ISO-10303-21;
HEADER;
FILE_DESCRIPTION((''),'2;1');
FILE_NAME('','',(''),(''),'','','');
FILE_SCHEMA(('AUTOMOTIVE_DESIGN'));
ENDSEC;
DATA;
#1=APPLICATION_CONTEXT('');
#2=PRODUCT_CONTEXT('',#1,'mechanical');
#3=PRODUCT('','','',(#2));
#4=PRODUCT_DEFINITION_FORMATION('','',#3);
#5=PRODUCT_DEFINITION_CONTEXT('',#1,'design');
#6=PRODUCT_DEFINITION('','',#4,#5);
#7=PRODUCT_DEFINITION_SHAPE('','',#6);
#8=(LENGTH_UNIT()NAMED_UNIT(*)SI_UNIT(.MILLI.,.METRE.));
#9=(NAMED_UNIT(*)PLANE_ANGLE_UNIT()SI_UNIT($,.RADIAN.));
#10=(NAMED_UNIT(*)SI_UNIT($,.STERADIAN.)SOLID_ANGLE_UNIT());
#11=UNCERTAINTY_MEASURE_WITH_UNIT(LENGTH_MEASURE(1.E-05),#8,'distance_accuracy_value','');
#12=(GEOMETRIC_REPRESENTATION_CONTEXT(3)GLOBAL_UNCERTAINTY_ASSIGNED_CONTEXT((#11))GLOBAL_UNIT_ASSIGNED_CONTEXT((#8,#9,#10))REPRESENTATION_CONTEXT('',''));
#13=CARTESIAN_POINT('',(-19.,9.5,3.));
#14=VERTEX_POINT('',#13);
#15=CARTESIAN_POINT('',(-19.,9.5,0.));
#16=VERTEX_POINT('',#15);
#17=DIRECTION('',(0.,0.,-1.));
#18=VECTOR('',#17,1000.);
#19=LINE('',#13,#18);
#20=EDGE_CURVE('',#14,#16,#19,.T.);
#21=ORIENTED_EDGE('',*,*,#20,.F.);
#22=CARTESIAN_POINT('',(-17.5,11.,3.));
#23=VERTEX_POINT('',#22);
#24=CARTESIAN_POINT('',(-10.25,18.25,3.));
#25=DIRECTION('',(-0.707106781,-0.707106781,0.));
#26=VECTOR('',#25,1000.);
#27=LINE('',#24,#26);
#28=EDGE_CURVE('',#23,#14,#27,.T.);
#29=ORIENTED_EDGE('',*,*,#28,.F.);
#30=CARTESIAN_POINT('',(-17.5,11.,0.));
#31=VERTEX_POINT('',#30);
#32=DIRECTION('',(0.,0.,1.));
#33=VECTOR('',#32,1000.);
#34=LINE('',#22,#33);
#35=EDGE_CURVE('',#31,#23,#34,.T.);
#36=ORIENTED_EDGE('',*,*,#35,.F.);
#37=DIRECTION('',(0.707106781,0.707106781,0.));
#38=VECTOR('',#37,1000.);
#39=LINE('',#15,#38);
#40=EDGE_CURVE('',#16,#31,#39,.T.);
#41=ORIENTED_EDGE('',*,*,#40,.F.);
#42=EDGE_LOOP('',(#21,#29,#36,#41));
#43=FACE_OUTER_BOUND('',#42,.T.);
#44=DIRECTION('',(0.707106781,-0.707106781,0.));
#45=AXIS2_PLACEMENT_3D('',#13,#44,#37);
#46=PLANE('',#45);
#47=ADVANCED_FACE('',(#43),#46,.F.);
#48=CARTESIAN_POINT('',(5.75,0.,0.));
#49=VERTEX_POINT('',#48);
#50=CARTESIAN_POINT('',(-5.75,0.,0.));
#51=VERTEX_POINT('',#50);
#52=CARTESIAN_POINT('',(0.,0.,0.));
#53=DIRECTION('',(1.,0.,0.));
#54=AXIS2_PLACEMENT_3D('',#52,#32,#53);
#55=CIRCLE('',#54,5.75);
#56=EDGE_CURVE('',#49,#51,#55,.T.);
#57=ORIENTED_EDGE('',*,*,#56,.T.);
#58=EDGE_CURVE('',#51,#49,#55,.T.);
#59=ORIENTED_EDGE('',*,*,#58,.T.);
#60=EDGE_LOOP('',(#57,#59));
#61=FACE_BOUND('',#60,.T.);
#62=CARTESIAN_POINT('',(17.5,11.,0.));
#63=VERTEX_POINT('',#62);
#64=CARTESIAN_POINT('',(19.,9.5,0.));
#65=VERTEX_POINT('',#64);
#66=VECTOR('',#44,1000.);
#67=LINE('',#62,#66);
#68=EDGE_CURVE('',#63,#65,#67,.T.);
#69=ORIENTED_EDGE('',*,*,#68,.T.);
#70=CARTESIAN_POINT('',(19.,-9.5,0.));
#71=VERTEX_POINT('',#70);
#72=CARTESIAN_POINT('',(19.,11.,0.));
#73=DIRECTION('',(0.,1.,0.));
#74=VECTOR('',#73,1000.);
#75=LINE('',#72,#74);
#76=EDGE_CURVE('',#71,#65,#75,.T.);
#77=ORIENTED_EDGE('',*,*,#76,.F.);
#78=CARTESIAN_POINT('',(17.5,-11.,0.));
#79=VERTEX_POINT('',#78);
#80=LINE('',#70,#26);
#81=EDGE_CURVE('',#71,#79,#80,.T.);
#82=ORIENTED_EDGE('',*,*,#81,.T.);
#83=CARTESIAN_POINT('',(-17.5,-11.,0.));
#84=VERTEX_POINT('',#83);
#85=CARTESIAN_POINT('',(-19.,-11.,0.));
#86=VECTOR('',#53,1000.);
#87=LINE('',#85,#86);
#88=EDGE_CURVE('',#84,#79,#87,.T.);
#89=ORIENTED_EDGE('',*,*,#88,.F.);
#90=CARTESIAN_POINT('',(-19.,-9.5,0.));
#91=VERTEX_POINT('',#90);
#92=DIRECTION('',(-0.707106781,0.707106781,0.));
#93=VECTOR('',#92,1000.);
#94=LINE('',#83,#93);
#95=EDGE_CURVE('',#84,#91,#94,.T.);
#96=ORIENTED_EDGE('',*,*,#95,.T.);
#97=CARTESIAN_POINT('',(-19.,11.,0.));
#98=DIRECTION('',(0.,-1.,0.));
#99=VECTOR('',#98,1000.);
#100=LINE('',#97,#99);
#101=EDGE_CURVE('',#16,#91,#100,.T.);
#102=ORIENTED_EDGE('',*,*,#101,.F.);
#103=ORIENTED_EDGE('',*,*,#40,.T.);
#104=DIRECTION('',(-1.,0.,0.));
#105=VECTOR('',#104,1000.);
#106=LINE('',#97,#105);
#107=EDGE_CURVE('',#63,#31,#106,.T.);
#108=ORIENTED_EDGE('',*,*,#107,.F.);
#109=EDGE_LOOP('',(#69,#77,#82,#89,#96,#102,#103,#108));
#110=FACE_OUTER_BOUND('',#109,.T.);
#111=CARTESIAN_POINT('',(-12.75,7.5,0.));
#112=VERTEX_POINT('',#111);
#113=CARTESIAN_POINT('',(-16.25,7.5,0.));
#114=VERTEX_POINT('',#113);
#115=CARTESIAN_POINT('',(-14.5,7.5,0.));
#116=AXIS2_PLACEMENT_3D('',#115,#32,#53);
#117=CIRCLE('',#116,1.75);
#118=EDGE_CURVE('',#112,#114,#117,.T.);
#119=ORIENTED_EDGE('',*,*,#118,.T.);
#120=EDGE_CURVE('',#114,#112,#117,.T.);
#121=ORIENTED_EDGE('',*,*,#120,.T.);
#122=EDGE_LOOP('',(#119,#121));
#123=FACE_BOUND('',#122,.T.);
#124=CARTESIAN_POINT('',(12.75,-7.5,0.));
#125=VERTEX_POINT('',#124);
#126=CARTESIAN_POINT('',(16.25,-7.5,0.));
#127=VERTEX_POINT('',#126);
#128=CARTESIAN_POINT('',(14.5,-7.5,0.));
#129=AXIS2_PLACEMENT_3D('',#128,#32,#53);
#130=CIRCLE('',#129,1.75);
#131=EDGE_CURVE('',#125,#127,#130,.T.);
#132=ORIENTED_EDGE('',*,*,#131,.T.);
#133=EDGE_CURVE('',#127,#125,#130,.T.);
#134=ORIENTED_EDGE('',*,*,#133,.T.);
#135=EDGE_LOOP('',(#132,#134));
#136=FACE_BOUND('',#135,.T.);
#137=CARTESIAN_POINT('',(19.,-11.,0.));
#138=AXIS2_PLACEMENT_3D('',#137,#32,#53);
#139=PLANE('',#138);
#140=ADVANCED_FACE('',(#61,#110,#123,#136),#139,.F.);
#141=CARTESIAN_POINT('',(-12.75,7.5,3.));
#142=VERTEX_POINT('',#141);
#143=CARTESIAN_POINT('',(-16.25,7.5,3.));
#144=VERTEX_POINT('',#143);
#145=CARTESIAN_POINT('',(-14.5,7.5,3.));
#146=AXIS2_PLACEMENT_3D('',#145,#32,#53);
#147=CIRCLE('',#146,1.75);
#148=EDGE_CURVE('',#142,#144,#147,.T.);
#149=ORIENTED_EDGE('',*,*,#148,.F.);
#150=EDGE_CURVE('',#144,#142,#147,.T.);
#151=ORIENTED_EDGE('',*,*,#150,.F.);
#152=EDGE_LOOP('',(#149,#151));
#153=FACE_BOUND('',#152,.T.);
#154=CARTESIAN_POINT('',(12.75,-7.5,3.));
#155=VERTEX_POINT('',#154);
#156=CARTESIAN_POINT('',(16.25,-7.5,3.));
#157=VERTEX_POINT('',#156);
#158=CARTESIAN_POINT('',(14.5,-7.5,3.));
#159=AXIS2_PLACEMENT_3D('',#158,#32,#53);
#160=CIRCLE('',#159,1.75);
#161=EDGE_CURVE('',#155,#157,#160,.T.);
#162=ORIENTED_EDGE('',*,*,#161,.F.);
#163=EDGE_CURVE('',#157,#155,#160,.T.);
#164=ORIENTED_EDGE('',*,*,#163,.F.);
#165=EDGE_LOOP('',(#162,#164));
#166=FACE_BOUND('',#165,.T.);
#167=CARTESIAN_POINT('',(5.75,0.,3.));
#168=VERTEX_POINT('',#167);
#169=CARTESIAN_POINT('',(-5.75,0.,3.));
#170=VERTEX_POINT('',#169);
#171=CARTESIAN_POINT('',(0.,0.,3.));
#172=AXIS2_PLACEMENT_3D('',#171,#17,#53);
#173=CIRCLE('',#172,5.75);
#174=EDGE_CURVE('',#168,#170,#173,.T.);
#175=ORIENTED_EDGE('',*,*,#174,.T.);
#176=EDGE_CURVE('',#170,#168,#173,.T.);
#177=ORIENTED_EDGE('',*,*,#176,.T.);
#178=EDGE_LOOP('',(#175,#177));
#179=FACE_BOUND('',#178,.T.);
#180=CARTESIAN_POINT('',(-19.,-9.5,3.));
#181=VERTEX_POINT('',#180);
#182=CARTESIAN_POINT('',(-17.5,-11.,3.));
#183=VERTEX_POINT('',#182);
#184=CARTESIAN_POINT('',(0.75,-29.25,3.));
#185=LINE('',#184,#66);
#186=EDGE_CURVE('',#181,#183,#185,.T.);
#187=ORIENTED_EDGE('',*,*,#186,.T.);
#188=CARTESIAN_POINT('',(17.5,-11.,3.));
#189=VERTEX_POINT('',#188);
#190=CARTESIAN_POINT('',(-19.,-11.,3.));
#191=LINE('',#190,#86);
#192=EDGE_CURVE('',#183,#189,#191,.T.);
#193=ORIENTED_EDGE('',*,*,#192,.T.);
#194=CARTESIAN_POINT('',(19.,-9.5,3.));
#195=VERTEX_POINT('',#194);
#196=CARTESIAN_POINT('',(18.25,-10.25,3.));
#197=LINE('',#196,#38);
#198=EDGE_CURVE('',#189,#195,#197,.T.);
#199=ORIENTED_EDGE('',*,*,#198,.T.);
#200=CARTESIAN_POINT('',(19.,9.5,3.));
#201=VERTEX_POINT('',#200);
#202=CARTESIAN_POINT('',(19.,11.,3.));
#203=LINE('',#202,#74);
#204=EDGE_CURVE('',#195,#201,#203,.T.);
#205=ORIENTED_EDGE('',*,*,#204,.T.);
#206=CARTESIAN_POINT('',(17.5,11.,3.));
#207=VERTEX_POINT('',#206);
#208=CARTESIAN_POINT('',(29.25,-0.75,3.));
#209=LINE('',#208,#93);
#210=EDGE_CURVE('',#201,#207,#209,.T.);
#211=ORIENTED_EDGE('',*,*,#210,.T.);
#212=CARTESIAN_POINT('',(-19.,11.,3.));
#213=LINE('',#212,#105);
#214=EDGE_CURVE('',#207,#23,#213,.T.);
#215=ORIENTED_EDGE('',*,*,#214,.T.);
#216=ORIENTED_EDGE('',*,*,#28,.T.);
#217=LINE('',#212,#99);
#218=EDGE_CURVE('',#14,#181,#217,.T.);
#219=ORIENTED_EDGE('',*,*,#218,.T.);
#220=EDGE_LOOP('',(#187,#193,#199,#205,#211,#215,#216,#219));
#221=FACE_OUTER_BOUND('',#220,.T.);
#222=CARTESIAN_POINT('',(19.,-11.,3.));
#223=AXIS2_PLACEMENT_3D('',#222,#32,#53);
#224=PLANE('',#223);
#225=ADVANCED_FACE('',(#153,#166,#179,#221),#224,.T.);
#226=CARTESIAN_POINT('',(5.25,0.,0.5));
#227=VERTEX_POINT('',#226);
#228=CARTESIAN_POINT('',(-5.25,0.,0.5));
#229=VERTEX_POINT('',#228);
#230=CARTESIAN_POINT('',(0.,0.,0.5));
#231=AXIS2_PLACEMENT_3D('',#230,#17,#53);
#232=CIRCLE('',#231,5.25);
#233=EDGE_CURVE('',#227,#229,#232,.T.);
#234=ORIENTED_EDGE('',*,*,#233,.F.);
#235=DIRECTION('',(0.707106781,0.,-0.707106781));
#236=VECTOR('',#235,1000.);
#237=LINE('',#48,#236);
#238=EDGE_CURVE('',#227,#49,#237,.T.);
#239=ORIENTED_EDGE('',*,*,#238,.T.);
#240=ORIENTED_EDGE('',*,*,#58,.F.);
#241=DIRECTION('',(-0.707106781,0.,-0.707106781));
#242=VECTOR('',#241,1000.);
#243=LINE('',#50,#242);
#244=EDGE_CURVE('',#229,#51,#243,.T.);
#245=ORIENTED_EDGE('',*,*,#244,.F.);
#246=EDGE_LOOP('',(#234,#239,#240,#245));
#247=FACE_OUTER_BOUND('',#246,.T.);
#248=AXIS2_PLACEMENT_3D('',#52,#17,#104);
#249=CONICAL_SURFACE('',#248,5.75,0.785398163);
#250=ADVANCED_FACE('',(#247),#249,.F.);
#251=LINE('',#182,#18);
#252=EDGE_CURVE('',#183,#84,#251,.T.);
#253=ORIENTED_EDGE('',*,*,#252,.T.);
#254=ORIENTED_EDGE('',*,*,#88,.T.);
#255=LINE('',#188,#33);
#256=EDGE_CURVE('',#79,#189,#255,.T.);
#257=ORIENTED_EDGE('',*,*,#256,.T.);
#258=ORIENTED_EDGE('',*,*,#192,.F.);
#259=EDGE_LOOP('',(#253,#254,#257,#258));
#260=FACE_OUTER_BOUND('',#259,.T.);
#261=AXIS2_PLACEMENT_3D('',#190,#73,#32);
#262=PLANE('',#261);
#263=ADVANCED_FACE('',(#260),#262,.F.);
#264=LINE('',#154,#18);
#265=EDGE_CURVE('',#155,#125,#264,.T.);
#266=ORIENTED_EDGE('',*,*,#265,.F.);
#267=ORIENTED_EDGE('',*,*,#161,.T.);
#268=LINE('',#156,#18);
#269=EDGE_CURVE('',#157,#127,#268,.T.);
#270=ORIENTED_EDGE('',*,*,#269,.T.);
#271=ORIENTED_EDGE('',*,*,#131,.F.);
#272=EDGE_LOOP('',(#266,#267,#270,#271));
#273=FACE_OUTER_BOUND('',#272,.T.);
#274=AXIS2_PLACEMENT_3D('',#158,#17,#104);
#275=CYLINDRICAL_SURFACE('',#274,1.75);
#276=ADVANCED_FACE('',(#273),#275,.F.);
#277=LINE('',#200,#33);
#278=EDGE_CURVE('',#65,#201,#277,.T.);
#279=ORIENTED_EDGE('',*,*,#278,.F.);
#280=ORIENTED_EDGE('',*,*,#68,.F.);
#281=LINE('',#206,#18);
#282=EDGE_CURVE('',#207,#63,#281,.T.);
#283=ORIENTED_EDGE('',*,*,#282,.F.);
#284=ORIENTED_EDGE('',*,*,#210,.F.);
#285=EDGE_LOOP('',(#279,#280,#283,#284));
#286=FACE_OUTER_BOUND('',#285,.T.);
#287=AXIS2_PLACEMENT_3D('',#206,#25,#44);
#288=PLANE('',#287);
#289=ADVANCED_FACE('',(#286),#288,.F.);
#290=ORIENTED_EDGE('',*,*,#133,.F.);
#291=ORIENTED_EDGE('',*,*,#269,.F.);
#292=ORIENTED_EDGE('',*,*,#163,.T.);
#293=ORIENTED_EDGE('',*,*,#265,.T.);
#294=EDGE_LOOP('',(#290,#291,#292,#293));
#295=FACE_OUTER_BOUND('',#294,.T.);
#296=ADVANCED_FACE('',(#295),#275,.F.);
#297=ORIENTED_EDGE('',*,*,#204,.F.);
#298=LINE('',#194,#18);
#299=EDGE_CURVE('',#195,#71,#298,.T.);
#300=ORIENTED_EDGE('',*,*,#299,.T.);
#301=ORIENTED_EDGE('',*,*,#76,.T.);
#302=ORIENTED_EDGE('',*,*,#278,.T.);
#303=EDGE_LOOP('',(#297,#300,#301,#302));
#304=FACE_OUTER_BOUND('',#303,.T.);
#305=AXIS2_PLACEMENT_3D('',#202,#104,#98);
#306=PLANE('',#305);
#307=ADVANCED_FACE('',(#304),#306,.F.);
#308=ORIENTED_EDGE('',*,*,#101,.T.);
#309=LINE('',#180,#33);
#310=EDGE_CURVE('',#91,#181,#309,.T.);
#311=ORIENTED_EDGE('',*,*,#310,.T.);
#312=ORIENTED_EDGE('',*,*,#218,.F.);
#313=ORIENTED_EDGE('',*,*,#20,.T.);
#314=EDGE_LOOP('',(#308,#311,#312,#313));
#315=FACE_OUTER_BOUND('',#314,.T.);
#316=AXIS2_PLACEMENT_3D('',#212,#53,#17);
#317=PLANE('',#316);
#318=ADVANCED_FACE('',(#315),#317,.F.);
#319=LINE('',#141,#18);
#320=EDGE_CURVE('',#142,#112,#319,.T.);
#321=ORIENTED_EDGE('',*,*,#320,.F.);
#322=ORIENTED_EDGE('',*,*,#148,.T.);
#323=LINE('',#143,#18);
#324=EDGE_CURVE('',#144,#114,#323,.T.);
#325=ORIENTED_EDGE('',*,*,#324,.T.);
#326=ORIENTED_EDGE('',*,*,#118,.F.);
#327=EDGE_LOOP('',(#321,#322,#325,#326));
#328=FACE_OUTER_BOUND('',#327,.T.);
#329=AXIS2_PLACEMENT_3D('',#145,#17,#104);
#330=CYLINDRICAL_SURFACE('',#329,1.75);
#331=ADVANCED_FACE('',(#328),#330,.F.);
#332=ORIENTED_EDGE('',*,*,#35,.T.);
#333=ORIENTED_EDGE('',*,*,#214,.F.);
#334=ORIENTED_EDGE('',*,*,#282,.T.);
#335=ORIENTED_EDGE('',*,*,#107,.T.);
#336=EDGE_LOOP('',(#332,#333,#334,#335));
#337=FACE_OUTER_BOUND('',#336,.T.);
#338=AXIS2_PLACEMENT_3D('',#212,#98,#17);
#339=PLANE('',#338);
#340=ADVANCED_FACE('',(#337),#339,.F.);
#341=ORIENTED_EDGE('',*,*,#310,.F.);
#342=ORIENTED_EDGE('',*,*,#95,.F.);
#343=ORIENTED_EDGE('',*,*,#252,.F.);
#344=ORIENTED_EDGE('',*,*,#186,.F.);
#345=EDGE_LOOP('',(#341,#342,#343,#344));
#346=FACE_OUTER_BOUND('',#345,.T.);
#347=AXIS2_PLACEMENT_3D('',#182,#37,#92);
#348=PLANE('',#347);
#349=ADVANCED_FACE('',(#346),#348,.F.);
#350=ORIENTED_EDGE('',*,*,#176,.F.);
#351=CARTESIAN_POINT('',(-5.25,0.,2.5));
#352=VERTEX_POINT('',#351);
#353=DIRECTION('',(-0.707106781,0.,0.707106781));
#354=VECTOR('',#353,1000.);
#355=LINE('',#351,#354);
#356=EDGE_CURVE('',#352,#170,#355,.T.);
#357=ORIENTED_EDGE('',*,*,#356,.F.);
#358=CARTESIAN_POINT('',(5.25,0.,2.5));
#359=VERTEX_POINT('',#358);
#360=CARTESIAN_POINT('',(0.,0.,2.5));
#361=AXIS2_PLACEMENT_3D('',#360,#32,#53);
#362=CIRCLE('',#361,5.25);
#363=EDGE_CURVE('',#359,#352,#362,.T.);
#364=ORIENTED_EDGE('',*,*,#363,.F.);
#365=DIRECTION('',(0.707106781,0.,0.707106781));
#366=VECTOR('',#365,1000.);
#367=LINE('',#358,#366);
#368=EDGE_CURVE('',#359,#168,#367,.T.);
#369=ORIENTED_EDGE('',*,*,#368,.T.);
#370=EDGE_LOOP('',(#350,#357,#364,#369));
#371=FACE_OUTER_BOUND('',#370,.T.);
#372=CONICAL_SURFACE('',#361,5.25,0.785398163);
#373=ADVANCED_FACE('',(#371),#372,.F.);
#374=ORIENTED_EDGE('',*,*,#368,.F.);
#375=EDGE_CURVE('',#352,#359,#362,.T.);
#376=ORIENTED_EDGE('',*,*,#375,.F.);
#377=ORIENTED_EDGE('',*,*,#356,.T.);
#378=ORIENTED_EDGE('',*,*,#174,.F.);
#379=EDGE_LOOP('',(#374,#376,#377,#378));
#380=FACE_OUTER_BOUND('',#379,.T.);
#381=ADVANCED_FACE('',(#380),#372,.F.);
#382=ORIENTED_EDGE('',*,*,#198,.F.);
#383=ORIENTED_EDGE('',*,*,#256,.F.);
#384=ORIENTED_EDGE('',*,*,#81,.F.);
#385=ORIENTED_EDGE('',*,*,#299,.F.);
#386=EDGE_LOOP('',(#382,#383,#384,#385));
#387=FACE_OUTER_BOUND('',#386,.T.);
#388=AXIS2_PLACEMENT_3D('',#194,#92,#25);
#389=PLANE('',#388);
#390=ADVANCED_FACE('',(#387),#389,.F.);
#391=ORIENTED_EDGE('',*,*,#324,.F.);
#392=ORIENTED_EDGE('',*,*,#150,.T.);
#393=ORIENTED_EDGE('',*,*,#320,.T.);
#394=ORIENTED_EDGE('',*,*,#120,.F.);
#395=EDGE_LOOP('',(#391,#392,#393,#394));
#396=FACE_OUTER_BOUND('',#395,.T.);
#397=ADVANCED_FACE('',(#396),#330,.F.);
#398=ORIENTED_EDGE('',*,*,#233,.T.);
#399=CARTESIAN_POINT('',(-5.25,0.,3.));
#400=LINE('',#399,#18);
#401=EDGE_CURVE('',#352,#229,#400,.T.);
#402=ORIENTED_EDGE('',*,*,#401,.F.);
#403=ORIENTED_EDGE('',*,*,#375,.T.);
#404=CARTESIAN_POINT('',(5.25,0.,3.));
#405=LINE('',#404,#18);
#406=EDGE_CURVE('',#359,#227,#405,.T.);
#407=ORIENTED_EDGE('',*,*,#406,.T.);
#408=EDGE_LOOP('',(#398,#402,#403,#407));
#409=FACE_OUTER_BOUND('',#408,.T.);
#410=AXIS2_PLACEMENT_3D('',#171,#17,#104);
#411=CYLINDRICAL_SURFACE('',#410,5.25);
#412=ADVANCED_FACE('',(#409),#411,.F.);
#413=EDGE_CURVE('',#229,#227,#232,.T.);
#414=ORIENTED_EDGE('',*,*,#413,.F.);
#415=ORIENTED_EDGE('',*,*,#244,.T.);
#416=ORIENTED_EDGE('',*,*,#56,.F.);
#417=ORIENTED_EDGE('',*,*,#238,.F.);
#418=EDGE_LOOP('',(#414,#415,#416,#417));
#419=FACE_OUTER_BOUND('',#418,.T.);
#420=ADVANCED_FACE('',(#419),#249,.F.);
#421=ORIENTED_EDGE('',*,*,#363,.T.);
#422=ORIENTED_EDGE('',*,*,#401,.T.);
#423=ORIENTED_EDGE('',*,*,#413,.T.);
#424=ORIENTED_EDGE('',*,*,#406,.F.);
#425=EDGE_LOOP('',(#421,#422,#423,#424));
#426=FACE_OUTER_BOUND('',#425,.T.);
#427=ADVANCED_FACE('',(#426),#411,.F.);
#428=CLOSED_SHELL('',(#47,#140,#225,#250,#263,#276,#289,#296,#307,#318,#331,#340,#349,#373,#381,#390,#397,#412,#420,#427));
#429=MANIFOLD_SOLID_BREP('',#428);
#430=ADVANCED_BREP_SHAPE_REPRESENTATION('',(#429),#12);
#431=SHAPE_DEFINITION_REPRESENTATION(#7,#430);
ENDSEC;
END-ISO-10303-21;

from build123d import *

# Parameters (mm, degrees)
SKETCH1_W           = 38
SKETCH1_H           = 22
SKETCH1_R           = 5.25
SKETCH1_R_2         = 1.75
BOSS_EXTRUDE1_DEPTH = 3
CHAMFER1_SIZE       = 1.5
CHAMFER2_SIZE       = 0.5


with BuildPart() as part:
    # Sketch1 → Boss-Extrude1 (new body)
    with BuildSketch(Plane.XY):
        Rectangle(SKETCH1_W, SKETCH1_H)
        Circle(SKETCH1_R, mode=Mode.SUBTRACT)
        with Locations((-14.5, 7.5)):
            Circle(SKETCH1_R_2, mode=Mode.SUBTRACT)
        with Locations((14.5, -7.5)):
            Circle(SKETCH1_R_2, mode=Mode.SUBTRACT)
    extrude(amount=BOSS_EXTRUDE1_DEPTH)

    # Chamfer1
    chamfer1_edges = [part.edges().sort_by_distance(p)[0] for p in [
        (19, -11, 1.5),
        (-19, -11, 1.5),
        (-19, 11, 1.5),
        (19, 11, 1.5),
    ]]
    chamfer(chamfer1_edges, length=CHAMFER1_SIZE)

    # Chamfer2
    chamfer2_edges = [part.edges().sort_by_distance(p)[0] for p in [
        (-5.25, 0, 0),
        (-5.25, 0, 3),
    ]]
    chamfer(chamfer2_edges, length=CHAMFER2_SIZE)


solid = part.part
